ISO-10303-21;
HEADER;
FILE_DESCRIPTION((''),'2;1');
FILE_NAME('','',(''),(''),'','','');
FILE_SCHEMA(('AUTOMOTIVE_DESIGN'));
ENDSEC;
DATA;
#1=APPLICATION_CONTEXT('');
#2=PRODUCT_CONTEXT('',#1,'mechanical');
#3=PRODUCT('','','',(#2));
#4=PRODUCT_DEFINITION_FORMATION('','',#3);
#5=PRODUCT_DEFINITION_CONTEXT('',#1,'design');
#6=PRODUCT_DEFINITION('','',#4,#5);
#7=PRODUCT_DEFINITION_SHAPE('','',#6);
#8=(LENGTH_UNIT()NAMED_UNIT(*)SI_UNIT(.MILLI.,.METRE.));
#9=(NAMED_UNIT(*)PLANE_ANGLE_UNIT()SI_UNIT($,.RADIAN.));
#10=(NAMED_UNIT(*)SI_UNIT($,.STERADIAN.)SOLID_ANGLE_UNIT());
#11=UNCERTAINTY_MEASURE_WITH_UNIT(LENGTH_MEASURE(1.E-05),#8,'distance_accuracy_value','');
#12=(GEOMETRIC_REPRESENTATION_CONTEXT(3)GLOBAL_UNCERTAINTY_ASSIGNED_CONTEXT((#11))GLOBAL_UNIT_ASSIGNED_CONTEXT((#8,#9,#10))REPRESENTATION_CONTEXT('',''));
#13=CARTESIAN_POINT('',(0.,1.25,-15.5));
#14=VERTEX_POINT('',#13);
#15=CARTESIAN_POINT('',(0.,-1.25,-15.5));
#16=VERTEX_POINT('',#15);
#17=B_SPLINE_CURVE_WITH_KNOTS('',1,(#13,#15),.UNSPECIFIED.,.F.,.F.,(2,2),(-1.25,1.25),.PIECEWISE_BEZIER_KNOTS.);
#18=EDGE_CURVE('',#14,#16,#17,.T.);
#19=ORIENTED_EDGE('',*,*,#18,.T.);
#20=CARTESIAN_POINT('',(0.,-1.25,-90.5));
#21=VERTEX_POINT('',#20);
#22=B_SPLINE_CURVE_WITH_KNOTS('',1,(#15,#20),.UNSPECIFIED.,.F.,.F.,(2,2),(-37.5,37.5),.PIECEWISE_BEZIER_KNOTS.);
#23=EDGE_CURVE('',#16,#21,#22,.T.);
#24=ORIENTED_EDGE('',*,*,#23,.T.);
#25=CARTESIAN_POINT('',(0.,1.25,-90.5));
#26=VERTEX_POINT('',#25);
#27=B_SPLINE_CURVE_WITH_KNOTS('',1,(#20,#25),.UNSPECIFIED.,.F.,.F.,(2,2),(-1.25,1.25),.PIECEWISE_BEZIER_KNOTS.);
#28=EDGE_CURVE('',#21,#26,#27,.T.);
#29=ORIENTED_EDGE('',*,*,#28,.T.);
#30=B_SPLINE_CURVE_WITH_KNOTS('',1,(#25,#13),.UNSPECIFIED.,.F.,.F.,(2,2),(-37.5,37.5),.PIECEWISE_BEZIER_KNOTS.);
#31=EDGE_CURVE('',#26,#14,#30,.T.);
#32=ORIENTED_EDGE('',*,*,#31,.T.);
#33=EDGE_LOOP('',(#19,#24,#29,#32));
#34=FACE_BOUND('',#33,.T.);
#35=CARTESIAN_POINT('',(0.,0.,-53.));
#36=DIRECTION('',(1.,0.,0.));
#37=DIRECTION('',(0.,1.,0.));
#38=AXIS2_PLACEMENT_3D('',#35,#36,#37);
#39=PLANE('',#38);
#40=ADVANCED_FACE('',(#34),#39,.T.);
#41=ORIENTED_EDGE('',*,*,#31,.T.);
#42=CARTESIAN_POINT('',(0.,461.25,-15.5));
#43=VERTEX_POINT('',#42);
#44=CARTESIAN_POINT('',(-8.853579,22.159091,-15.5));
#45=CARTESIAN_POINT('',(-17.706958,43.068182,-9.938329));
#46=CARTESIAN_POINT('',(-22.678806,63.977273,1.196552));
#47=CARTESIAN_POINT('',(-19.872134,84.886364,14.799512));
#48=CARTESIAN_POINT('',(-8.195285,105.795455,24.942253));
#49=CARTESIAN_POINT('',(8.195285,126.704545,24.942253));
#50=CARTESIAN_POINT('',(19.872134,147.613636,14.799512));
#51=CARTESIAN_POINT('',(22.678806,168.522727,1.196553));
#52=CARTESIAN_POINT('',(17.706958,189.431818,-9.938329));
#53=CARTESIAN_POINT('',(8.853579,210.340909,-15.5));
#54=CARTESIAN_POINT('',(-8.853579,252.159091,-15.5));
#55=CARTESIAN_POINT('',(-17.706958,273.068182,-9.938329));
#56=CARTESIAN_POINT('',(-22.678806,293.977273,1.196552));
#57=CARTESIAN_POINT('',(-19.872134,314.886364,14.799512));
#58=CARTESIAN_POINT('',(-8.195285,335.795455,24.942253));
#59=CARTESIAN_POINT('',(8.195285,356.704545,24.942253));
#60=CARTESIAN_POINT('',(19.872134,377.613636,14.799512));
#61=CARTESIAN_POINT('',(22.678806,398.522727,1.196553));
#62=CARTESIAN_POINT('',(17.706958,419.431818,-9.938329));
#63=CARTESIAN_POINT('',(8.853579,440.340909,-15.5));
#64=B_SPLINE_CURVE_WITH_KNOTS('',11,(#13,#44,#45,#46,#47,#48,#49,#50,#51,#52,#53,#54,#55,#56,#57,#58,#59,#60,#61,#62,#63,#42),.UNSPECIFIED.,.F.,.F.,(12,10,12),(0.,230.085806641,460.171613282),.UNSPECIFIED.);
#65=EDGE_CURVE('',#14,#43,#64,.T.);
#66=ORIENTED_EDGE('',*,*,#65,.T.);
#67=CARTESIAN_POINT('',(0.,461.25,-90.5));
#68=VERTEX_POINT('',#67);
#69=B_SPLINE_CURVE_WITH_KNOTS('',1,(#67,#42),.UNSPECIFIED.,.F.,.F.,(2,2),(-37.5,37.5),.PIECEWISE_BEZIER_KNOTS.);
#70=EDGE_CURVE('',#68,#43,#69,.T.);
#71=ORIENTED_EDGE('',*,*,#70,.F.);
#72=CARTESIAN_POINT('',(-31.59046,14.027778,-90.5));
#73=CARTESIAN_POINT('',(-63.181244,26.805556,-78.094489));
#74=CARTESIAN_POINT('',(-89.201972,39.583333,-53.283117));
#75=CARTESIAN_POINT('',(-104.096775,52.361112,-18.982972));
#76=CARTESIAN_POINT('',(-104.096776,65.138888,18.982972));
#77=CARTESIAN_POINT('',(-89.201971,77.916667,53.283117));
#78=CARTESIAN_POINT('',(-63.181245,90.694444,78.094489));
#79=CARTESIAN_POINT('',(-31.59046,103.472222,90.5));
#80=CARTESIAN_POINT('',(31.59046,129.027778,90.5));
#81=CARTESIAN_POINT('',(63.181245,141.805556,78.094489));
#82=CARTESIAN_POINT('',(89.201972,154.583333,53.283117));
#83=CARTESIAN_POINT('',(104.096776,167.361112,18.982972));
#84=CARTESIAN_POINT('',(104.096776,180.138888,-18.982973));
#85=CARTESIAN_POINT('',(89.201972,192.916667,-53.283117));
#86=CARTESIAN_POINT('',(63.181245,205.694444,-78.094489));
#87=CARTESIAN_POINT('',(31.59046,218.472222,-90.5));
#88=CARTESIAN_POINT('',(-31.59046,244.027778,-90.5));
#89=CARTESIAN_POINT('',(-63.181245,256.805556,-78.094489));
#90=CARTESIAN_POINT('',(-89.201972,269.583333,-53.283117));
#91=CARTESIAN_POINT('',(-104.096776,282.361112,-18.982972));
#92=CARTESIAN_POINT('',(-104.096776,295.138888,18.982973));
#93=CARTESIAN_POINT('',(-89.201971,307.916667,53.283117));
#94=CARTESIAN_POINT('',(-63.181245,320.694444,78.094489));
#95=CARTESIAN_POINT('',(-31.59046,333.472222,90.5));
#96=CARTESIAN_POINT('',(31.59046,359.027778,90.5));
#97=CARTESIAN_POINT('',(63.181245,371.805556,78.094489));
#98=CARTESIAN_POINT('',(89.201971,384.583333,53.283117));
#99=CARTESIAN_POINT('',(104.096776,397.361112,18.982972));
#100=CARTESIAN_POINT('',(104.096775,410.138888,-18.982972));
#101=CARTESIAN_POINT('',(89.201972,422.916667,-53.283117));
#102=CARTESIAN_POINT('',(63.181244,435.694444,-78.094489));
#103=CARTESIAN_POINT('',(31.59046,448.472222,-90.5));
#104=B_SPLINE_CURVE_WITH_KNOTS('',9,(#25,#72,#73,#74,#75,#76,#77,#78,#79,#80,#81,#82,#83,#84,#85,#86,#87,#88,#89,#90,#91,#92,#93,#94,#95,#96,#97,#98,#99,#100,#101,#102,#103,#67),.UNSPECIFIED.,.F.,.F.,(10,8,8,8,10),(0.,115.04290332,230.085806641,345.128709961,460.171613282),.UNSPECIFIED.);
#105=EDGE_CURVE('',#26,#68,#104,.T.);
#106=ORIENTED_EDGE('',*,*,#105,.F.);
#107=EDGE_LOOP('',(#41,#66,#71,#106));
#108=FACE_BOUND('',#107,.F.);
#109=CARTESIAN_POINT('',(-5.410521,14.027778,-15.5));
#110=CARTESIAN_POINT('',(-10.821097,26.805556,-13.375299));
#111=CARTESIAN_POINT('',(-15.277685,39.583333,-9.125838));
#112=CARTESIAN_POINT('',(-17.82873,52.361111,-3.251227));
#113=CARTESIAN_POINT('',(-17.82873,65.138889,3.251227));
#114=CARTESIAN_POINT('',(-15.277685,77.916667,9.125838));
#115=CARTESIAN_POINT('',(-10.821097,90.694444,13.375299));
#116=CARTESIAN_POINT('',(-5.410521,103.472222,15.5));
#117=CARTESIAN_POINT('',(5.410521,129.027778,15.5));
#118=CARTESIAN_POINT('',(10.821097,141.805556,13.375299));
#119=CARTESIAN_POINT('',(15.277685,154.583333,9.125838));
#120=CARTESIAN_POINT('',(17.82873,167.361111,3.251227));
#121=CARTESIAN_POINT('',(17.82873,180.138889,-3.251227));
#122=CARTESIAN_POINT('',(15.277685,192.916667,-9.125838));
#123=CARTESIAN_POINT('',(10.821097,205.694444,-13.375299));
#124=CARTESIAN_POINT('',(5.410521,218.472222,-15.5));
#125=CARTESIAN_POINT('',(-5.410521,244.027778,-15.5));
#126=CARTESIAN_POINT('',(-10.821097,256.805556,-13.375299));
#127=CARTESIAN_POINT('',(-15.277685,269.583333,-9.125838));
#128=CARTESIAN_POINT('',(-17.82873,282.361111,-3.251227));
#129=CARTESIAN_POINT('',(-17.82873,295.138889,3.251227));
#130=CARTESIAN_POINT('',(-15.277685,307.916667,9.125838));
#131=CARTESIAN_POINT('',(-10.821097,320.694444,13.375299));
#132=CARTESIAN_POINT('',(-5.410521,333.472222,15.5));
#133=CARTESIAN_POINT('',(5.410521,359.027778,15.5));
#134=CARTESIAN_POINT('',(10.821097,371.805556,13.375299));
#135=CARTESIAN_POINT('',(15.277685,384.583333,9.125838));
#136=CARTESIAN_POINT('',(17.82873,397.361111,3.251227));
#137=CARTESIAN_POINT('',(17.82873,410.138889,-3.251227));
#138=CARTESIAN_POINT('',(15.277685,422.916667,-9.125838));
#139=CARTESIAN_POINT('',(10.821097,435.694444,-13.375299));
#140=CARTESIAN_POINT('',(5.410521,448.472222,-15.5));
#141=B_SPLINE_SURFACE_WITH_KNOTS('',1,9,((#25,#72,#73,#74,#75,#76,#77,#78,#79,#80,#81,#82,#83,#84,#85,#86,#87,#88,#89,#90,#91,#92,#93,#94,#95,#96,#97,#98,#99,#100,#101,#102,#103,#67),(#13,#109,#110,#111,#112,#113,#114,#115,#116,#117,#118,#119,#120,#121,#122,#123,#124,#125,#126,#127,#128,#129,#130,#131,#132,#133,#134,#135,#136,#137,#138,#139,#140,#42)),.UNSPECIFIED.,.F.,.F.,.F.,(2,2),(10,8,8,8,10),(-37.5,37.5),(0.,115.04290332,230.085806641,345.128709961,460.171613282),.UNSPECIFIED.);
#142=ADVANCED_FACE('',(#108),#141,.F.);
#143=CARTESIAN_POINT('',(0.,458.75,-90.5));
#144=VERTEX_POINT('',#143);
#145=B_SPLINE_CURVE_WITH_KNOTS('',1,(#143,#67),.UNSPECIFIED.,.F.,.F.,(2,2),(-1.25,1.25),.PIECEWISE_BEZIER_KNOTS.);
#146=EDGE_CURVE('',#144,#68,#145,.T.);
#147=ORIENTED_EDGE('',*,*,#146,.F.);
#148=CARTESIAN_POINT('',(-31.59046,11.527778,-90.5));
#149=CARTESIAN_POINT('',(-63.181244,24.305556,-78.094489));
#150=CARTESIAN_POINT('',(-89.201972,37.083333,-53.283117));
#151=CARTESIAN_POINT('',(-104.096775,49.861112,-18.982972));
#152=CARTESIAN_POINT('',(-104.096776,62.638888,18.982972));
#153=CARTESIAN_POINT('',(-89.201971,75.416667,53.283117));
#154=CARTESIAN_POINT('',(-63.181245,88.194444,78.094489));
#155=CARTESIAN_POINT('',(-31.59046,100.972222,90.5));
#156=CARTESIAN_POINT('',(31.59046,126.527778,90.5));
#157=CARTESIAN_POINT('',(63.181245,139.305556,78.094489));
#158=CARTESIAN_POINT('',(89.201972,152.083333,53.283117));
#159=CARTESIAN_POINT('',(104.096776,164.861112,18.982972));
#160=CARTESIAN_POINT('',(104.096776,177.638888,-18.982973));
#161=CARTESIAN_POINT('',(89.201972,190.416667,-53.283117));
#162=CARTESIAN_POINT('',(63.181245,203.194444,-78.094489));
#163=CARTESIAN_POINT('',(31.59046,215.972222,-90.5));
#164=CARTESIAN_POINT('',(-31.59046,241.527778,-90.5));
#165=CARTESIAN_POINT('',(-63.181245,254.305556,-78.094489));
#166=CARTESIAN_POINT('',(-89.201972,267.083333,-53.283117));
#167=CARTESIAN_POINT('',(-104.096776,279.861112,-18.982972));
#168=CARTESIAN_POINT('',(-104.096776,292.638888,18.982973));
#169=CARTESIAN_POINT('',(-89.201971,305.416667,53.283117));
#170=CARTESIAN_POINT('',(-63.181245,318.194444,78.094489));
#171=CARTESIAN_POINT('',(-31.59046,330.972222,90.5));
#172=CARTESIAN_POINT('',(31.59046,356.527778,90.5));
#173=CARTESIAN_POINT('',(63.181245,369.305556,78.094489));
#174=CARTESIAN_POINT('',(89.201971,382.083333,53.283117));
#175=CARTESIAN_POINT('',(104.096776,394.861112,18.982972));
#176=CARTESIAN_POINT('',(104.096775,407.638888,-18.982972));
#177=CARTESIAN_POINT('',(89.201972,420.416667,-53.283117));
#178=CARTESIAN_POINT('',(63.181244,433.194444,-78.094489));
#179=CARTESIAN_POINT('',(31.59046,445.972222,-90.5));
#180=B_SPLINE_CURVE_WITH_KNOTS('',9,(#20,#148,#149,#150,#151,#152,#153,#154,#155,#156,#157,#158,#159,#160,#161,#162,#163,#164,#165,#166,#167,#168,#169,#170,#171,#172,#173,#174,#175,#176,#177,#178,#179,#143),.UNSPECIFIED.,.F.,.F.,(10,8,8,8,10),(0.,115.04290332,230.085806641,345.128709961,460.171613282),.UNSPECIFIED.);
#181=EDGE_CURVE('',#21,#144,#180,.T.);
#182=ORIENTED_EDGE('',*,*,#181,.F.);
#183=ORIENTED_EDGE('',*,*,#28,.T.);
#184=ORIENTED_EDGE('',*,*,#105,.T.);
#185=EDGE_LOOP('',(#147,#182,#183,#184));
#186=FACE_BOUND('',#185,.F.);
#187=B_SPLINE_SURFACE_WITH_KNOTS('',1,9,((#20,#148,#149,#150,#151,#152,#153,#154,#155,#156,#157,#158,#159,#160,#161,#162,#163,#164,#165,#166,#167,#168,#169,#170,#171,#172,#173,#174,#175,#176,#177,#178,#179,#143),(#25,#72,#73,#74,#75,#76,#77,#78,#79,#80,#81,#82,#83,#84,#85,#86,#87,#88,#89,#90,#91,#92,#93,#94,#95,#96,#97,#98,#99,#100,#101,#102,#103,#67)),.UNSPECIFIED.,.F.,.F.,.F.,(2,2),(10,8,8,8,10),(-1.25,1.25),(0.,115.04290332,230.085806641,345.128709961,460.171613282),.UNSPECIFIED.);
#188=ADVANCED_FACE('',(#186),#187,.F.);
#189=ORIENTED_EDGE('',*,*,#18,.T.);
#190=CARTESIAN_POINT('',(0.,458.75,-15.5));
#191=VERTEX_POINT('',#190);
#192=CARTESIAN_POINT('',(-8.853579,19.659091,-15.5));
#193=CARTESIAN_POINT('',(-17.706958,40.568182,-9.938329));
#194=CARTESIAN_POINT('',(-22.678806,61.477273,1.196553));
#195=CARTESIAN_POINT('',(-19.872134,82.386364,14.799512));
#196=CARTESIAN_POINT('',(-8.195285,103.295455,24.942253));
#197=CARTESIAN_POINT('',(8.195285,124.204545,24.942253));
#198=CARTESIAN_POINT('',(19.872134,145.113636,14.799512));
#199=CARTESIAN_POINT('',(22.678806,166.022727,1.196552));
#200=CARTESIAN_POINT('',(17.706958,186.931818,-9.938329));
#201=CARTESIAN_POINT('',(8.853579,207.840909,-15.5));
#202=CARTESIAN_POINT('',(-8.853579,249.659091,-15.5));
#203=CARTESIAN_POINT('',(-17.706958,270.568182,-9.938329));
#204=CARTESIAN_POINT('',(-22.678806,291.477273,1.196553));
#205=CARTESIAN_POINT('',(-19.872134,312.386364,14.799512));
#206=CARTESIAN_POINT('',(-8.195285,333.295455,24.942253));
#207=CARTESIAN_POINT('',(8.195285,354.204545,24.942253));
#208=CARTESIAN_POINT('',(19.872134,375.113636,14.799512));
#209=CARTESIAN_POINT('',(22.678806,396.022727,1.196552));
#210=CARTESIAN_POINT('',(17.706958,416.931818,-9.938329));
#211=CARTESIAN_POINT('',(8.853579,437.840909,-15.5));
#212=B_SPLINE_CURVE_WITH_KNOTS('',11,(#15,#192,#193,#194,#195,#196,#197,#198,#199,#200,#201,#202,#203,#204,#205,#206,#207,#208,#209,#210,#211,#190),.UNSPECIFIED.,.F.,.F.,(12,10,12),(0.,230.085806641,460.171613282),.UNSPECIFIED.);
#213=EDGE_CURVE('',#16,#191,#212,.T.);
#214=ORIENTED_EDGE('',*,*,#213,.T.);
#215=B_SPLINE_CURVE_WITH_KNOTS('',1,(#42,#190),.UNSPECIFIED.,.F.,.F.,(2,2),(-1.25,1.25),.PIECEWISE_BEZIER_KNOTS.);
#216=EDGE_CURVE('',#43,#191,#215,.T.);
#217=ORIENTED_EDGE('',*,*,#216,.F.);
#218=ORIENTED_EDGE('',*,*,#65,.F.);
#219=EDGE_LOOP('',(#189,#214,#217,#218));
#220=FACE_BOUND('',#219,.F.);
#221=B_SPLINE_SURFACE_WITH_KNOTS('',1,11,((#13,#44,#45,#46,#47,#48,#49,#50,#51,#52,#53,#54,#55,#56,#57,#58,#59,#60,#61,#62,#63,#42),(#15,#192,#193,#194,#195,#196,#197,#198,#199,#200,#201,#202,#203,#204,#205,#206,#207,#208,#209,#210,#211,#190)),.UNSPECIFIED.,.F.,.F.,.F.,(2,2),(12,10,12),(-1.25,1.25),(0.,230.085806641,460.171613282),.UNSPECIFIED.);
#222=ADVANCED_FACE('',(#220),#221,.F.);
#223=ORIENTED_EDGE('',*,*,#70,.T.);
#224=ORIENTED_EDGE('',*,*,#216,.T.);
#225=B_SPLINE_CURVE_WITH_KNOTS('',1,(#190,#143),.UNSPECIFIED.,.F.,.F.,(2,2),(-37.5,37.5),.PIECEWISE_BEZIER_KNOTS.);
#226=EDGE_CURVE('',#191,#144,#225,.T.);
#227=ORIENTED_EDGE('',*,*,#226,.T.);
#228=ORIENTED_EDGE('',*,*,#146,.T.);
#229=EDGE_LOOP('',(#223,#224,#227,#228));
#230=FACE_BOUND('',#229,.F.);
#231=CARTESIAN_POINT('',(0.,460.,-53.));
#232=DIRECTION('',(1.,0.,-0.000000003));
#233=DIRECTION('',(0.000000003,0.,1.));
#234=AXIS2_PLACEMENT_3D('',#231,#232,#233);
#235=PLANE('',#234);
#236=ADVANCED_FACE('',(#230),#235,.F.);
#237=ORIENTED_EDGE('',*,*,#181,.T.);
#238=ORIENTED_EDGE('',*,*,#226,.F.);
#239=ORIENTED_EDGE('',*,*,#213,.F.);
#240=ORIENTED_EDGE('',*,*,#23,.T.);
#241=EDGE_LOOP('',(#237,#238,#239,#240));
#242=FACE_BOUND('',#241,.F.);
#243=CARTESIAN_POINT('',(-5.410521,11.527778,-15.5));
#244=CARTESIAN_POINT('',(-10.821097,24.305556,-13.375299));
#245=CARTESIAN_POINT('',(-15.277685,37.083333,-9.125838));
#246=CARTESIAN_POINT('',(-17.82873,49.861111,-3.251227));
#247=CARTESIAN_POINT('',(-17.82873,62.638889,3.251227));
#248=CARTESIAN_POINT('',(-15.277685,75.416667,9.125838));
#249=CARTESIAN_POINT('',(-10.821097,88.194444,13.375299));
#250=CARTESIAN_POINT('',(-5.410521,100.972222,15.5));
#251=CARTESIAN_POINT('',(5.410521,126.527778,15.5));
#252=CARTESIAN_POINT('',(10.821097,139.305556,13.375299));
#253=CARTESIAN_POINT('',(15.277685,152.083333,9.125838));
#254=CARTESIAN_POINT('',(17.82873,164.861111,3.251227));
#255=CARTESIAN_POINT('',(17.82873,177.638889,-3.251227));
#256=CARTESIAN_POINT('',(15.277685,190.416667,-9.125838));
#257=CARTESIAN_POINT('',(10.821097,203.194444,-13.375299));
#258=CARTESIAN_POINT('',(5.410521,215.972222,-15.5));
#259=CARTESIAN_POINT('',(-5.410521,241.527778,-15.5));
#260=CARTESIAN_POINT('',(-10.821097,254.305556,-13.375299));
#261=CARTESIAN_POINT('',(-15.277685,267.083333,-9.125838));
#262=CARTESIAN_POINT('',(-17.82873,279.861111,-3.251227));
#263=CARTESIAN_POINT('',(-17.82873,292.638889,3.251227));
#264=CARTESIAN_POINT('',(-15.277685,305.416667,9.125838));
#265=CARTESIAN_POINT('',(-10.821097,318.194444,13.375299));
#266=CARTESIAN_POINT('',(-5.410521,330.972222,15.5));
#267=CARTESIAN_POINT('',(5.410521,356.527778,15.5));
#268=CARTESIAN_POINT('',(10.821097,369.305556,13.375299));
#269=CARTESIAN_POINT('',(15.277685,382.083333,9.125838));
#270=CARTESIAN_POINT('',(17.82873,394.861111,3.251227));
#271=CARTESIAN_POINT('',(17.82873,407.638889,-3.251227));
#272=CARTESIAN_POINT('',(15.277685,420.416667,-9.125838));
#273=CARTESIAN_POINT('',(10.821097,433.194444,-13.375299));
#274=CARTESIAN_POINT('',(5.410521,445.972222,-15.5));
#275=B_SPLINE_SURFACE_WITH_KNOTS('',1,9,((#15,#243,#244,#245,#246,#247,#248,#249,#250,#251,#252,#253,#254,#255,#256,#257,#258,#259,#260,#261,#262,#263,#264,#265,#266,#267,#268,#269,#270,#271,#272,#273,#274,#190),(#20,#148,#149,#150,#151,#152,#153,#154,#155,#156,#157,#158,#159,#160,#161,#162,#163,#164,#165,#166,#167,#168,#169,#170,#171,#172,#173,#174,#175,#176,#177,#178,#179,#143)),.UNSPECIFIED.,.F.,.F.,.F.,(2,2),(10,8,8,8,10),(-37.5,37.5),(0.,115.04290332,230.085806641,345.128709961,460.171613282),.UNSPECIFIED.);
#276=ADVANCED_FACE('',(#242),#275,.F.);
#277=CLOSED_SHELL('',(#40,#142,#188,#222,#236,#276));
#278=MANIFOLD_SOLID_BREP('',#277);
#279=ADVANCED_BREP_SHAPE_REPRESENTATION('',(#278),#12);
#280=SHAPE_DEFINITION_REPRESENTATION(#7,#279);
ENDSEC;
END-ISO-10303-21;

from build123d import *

# Parameters (mm, degrees)
SWEEP_14_PITCH       = 230
SWEEP_14_HEIGHT      = 460
SWEEP_14_RADIUS      = 15
SWEEP_14_START_ANGLE = -180
SKETCH_11_W          = 75
SKETCH_11_H          = 2.5


with BuildPart() as part:
    # 扫描14: sweep along a helix
    with BuildLine() as sweep_14_path:
        add(Helix(SWEEP_14_PITCH, SWEEP_14_HEIGHT, SWEEP_14_RADIUS, center=(0, 0, 0), direction=(0, 1, 0), mode=Mode.PRIVATE).rotate(Axis((0, 0, 0), (0, 1, 0)), SWEEP_14_START_ANGLE))
    # 草图11 → 扫描14 (sweep)
    with BuildSketch(Plane(origin=(0, 0, 0), x_dir=(0, 0, -1), z_dir=(1, 0, 0))):
        with Locations((53, 0)):
            Rectangle(SKETCH_11_W, SKETCH_11_H)
    sweep(path=sweep_14_path.line, is_frenet=True)


solid = part.part
